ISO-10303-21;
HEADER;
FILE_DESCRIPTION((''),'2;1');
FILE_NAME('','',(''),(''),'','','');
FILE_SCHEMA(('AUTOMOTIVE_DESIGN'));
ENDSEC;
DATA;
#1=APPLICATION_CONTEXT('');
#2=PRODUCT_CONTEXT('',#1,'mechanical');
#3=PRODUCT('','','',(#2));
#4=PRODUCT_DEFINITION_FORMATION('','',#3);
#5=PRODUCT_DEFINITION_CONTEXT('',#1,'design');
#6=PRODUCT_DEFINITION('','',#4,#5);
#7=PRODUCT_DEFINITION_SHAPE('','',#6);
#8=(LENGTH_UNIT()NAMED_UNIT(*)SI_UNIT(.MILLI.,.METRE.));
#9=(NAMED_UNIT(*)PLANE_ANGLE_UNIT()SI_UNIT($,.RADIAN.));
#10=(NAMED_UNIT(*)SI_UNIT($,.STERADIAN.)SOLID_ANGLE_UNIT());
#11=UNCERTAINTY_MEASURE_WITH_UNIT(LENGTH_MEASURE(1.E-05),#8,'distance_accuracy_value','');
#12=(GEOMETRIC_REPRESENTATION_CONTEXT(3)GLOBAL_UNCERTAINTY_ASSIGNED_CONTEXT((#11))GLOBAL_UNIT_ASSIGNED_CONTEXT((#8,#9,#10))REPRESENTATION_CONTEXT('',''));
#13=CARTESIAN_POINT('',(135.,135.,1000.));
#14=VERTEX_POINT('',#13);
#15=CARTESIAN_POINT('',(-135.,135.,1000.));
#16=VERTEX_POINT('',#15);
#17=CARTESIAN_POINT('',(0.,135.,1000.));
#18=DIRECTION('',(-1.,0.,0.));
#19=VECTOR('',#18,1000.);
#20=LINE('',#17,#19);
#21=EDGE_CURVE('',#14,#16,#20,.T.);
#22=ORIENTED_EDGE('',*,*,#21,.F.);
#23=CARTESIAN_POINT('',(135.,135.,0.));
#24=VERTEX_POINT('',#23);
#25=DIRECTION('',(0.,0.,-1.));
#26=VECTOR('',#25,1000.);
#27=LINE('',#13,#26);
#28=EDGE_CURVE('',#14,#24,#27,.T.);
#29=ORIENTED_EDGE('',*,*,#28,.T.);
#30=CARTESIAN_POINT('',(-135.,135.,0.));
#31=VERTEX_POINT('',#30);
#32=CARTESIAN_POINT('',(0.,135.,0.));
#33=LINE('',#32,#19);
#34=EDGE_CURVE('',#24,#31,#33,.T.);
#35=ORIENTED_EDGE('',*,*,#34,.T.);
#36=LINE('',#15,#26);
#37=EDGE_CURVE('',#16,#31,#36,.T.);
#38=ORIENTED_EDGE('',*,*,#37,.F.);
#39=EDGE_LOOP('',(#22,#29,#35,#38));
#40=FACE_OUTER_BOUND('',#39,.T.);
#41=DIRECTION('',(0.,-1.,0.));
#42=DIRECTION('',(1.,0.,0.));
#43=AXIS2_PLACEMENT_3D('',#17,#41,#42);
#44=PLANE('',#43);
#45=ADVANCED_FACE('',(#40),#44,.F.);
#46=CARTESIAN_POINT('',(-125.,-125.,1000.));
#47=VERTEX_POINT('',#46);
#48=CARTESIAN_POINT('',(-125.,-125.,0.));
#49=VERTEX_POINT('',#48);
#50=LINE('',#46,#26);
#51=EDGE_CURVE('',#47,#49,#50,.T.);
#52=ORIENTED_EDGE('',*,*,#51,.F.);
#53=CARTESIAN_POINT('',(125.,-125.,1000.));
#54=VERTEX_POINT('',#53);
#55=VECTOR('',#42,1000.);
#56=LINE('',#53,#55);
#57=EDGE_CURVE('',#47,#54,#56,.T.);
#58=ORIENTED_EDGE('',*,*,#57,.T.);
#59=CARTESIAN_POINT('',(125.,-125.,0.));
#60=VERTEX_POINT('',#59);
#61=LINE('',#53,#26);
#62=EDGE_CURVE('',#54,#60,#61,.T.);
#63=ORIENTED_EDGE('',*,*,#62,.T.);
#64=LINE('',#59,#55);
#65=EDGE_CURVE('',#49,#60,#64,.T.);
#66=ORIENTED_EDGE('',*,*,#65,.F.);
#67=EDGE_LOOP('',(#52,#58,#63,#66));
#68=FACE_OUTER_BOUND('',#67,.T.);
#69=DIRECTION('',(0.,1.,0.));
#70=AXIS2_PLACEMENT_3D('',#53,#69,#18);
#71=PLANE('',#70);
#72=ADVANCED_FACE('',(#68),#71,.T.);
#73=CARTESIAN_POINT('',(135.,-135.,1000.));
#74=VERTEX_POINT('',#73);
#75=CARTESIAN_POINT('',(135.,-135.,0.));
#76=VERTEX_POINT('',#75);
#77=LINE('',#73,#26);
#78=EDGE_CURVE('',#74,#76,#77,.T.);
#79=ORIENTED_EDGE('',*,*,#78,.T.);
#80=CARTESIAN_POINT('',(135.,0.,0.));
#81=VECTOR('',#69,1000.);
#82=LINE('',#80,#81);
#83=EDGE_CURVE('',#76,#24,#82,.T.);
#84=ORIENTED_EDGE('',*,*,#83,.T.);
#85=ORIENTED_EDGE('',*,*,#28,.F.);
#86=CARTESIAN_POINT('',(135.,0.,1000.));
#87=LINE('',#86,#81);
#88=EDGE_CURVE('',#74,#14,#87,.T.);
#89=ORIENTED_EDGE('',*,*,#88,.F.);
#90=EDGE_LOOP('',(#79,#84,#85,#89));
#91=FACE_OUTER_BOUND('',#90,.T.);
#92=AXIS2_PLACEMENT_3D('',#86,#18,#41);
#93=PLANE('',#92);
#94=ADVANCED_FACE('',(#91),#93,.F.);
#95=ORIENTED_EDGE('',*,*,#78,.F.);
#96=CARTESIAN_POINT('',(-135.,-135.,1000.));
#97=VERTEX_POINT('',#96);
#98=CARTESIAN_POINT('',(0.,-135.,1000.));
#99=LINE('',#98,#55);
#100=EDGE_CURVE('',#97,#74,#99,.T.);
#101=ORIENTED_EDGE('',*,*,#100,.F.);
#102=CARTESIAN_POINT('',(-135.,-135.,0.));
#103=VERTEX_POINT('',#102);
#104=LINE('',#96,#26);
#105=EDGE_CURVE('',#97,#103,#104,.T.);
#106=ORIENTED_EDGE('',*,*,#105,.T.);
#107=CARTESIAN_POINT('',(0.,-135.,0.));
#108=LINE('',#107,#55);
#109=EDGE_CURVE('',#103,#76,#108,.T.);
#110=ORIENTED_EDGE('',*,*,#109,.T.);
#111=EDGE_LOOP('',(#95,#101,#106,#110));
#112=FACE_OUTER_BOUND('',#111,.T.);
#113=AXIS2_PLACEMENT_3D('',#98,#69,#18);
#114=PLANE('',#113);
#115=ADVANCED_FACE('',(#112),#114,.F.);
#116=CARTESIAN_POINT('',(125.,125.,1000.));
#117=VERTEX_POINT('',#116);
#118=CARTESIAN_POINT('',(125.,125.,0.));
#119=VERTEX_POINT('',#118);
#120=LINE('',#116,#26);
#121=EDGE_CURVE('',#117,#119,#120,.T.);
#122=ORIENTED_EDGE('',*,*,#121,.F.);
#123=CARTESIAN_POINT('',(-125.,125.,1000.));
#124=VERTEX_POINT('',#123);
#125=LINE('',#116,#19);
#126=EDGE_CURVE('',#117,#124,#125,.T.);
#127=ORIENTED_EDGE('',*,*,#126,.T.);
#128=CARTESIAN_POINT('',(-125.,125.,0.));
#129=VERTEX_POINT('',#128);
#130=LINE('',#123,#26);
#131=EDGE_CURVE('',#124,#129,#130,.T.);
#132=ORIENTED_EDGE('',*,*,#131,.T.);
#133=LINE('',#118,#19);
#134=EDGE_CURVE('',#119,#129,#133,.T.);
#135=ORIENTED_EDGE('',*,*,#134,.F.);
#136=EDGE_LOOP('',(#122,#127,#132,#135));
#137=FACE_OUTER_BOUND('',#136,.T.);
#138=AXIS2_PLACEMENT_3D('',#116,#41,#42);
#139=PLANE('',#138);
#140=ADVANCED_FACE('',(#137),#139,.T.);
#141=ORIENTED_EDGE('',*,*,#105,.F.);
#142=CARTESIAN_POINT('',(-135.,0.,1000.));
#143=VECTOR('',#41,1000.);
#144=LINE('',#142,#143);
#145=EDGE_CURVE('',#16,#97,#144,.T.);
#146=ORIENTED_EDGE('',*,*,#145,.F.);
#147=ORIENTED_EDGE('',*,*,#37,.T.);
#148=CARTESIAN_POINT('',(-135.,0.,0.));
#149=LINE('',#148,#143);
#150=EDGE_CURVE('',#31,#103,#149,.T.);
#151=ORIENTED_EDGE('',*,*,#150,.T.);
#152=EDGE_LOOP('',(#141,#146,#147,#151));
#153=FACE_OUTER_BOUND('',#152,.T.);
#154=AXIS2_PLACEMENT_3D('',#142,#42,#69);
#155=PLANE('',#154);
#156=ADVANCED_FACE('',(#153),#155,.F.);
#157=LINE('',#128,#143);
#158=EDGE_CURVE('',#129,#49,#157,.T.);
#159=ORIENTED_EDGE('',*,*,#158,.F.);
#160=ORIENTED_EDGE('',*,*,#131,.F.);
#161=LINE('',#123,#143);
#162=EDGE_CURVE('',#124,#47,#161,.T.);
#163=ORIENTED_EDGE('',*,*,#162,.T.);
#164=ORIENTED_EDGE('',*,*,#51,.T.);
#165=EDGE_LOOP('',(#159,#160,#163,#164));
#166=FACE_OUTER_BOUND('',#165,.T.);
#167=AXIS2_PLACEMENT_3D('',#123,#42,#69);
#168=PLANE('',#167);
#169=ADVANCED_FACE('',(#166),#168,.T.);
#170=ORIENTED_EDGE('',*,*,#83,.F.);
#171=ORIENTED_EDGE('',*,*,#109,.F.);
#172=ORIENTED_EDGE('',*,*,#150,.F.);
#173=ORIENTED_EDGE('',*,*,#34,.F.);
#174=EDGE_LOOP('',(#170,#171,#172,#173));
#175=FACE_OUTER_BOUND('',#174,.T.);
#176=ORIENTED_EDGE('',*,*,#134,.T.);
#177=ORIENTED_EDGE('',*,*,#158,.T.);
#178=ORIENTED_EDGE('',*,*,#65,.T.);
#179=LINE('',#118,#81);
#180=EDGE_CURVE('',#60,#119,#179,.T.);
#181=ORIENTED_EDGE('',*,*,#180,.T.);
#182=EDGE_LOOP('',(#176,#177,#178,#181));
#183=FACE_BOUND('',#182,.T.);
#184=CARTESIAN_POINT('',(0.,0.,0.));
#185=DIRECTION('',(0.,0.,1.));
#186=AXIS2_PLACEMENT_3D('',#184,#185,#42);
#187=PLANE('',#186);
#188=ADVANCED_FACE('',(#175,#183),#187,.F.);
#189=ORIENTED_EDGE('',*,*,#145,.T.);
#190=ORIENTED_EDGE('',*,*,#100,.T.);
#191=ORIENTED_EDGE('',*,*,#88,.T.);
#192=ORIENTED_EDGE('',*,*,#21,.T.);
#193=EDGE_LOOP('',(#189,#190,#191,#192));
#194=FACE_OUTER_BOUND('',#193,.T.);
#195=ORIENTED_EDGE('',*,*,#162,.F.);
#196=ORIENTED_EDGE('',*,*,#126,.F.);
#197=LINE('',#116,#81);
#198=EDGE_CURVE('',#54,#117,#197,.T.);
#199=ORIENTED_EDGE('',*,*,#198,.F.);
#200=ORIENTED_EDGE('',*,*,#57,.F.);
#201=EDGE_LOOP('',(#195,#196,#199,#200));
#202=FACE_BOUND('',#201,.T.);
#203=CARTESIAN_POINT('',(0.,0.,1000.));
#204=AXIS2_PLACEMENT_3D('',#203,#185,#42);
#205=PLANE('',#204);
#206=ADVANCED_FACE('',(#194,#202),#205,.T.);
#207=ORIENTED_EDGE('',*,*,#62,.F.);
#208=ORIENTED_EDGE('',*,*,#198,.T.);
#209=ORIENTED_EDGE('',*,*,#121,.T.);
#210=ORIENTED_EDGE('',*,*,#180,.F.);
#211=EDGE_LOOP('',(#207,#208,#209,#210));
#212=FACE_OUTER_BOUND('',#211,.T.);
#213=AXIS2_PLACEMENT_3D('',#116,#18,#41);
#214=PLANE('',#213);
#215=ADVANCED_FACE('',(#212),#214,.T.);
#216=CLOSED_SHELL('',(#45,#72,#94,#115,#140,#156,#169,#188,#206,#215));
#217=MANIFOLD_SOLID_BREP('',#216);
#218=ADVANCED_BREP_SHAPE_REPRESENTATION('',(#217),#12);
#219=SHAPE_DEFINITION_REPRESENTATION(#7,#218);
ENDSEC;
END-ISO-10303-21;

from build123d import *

# Parameters (mm, degrees)
SKETCH1_W           = 270
SKETCH1_H           = 270
SKETCH1_W_2         = 250
SKETCH1_H_2         = 250
EXTRUDE_THIN1_DEPTH = 1000


with BuildPart() as part:
    # Sketch1 → Extrude-Thin1 (new body)
    with BuildSketch(Plane.XY):
        Rectangle(SKETCH1_W, SKETCH1_H)
        Rectangle(SKETCH1_W_2, SKETCH1_H_2, mode=Mode.SUBTRACT)
    extrude(amount=EXTRUDE_THIN1_DEPTH)


solid = part.part
